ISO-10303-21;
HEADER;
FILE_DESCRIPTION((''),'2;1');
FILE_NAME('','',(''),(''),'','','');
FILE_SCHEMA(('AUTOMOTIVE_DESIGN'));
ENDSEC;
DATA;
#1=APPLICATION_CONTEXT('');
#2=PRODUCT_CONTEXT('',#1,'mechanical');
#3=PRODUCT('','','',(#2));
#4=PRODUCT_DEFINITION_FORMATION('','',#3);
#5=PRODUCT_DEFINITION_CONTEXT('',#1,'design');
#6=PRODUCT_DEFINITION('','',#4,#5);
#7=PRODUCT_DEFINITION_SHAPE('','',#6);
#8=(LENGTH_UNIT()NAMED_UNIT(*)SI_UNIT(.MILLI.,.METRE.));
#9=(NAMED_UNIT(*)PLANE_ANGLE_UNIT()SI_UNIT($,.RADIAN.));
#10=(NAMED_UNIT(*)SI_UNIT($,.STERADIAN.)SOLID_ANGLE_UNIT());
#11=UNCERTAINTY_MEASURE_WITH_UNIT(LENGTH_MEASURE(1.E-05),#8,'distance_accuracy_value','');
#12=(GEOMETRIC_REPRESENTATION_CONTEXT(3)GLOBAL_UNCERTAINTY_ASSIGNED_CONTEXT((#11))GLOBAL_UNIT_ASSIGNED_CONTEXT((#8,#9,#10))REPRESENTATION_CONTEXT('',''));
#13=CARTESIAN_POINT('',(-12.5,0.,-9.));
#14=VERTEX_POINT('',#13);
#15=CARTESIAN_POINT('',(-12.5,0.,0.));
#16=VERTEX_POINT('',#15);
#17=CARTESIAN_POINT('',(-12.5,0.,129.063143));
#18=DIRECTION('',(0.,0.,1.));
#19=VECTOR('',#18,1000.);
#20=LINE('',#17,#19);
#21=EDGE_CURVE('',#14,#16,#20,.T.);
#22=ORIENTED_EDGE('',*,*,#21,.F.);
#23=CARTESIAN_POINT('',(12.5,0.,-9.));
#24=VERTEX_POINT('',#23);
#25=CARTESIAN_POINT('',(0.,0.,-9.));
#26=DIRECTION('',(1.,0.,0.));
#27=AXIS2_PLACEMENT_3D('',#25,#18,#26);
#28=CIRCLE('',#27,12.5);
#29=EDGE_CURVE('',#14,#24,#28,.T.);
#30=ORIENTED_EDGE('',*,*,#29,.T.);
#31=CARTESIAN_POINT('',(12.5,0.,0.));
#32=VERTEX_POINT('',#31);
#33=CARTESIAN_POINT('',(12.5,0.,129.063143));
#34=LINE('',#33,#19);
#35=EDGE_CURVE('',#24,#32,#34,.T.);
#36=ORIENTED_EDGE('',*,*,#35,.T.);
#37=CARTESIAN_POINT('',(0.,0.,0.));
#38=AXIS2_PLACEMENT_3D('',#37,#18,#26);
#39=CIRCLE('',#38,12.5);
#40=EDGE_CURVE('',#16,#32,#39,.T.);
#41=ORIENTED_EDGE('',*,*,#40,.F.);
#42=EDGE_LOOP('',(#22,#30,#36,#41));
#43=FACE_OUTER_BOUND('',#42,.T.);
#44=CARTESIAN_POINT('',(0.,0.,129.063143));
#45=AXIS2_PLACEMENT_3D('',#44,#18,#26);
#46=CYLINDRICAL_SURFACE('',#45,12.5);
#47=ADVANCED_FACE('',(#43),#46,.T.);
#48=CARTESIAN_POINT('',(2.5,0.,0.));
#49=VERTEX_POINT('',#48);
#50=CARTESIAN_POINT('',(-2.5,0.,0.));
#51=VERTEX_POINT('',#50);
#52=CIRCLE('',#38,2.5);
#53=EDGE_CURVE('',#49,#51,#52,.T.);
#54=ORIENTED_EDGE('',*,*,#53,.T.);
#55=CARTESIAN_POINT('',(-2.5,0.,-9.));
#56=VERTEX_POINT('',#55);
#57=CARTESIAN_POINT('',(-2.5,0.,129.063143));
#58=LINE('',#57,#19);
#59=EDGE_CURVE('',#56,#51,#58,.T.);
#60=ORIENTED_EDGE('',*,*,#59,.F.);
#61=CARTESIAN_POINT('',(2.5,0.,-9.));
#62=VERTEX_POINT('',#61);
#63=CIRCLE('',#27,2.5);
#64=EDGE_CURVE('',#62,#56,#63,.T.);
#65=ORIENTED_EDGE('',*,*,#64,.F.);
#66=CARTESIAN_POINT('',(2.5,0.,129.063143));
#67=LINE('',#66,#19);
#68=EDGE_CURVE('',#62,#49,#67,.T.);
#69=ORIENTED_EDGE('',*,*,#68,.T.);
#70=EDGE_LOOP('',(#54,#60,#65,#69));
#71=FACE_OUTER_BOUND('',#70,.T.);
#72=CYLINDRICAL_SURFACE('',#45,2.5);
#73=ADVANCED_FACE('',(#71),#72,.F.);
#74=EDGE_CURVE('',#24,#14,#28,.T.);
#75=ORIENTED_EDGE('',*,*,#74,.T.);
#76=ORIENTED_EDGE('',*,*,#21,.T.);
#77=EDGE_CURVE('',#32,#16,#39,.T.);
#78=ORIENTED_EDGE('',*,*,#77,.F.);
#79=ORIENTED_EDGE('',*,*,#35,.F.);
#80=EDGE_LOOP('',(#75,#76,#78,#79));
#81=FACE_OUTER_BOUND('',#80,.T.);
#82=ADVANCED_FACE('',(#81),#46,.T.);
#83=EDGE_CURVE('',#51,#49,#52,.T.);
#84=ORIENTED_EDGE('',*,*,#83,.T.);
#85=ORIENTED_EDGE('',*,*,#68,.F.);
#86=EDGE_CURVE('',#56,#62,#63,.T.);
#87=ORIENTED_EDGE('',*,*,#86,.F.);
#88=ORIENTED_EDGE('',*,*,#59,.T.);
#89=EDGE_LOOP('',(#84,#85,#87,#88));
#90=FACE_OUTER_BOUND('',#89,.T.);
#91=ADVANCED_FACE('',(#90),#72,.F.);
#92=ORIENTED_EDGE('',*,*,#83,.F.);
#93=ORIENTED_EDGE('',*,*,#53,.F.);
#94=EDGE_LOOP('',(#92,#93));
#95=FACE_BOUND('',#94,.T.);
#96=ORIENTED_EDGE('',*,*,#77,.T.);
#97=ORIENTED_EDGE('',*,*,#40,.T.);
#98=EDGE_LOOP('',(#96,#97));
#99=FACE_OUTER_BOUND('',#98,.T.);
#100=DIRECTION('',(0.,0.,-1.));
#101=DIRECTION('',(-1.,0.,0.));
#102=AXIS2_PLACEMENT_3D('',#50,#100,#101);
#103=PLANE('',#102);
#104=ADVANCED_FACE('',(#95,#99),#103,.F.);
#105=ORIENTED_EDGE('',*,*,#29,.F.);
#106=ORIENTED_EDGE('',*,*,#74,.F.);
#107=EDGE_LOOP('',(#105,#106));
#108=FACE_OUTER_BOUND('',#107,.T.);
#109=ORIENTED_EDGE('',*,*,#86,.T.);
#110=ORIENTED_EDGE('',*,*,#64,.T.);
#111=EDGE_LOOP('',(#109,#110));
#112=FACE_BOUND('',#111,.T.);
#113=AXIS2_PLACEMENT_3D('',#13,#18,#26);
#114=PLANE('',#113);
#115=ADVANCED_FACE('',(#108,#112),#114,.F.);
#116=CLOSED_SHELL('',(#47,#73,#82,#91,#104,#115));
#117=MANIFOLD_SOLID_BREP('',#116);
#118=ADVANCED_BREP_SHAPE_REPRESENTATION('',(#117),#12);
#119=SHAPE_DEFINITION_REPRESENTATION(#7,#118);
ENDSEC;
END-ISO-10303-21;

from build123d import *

# Parameters (mm, degrees)
SKETCH_1_W = 10
SKETCH_1_H = 9


with BuildPart() as part:
    # 草图1 → 旋转1 (revolve)
    with BuildSketch(Plane(origin=(0, 0, 0), x_dir=(1, 0, 0), z_dir=(0, 1, 0)), mode=Mode.PRIVATE) as revolve_1_sk:
        with Locations((-7.5, 4.5)):
            Rectangle(SKETCH_1_W, SKETCH_1_H)
    revolve(revolve_1_sk.sketch.rotate(Axis((0, 0, 129.063142874), (0, 0, -1)), 180), axis=Axis((0, 0, 129.063142874), (0, 0, -1)))


solid = part.part
